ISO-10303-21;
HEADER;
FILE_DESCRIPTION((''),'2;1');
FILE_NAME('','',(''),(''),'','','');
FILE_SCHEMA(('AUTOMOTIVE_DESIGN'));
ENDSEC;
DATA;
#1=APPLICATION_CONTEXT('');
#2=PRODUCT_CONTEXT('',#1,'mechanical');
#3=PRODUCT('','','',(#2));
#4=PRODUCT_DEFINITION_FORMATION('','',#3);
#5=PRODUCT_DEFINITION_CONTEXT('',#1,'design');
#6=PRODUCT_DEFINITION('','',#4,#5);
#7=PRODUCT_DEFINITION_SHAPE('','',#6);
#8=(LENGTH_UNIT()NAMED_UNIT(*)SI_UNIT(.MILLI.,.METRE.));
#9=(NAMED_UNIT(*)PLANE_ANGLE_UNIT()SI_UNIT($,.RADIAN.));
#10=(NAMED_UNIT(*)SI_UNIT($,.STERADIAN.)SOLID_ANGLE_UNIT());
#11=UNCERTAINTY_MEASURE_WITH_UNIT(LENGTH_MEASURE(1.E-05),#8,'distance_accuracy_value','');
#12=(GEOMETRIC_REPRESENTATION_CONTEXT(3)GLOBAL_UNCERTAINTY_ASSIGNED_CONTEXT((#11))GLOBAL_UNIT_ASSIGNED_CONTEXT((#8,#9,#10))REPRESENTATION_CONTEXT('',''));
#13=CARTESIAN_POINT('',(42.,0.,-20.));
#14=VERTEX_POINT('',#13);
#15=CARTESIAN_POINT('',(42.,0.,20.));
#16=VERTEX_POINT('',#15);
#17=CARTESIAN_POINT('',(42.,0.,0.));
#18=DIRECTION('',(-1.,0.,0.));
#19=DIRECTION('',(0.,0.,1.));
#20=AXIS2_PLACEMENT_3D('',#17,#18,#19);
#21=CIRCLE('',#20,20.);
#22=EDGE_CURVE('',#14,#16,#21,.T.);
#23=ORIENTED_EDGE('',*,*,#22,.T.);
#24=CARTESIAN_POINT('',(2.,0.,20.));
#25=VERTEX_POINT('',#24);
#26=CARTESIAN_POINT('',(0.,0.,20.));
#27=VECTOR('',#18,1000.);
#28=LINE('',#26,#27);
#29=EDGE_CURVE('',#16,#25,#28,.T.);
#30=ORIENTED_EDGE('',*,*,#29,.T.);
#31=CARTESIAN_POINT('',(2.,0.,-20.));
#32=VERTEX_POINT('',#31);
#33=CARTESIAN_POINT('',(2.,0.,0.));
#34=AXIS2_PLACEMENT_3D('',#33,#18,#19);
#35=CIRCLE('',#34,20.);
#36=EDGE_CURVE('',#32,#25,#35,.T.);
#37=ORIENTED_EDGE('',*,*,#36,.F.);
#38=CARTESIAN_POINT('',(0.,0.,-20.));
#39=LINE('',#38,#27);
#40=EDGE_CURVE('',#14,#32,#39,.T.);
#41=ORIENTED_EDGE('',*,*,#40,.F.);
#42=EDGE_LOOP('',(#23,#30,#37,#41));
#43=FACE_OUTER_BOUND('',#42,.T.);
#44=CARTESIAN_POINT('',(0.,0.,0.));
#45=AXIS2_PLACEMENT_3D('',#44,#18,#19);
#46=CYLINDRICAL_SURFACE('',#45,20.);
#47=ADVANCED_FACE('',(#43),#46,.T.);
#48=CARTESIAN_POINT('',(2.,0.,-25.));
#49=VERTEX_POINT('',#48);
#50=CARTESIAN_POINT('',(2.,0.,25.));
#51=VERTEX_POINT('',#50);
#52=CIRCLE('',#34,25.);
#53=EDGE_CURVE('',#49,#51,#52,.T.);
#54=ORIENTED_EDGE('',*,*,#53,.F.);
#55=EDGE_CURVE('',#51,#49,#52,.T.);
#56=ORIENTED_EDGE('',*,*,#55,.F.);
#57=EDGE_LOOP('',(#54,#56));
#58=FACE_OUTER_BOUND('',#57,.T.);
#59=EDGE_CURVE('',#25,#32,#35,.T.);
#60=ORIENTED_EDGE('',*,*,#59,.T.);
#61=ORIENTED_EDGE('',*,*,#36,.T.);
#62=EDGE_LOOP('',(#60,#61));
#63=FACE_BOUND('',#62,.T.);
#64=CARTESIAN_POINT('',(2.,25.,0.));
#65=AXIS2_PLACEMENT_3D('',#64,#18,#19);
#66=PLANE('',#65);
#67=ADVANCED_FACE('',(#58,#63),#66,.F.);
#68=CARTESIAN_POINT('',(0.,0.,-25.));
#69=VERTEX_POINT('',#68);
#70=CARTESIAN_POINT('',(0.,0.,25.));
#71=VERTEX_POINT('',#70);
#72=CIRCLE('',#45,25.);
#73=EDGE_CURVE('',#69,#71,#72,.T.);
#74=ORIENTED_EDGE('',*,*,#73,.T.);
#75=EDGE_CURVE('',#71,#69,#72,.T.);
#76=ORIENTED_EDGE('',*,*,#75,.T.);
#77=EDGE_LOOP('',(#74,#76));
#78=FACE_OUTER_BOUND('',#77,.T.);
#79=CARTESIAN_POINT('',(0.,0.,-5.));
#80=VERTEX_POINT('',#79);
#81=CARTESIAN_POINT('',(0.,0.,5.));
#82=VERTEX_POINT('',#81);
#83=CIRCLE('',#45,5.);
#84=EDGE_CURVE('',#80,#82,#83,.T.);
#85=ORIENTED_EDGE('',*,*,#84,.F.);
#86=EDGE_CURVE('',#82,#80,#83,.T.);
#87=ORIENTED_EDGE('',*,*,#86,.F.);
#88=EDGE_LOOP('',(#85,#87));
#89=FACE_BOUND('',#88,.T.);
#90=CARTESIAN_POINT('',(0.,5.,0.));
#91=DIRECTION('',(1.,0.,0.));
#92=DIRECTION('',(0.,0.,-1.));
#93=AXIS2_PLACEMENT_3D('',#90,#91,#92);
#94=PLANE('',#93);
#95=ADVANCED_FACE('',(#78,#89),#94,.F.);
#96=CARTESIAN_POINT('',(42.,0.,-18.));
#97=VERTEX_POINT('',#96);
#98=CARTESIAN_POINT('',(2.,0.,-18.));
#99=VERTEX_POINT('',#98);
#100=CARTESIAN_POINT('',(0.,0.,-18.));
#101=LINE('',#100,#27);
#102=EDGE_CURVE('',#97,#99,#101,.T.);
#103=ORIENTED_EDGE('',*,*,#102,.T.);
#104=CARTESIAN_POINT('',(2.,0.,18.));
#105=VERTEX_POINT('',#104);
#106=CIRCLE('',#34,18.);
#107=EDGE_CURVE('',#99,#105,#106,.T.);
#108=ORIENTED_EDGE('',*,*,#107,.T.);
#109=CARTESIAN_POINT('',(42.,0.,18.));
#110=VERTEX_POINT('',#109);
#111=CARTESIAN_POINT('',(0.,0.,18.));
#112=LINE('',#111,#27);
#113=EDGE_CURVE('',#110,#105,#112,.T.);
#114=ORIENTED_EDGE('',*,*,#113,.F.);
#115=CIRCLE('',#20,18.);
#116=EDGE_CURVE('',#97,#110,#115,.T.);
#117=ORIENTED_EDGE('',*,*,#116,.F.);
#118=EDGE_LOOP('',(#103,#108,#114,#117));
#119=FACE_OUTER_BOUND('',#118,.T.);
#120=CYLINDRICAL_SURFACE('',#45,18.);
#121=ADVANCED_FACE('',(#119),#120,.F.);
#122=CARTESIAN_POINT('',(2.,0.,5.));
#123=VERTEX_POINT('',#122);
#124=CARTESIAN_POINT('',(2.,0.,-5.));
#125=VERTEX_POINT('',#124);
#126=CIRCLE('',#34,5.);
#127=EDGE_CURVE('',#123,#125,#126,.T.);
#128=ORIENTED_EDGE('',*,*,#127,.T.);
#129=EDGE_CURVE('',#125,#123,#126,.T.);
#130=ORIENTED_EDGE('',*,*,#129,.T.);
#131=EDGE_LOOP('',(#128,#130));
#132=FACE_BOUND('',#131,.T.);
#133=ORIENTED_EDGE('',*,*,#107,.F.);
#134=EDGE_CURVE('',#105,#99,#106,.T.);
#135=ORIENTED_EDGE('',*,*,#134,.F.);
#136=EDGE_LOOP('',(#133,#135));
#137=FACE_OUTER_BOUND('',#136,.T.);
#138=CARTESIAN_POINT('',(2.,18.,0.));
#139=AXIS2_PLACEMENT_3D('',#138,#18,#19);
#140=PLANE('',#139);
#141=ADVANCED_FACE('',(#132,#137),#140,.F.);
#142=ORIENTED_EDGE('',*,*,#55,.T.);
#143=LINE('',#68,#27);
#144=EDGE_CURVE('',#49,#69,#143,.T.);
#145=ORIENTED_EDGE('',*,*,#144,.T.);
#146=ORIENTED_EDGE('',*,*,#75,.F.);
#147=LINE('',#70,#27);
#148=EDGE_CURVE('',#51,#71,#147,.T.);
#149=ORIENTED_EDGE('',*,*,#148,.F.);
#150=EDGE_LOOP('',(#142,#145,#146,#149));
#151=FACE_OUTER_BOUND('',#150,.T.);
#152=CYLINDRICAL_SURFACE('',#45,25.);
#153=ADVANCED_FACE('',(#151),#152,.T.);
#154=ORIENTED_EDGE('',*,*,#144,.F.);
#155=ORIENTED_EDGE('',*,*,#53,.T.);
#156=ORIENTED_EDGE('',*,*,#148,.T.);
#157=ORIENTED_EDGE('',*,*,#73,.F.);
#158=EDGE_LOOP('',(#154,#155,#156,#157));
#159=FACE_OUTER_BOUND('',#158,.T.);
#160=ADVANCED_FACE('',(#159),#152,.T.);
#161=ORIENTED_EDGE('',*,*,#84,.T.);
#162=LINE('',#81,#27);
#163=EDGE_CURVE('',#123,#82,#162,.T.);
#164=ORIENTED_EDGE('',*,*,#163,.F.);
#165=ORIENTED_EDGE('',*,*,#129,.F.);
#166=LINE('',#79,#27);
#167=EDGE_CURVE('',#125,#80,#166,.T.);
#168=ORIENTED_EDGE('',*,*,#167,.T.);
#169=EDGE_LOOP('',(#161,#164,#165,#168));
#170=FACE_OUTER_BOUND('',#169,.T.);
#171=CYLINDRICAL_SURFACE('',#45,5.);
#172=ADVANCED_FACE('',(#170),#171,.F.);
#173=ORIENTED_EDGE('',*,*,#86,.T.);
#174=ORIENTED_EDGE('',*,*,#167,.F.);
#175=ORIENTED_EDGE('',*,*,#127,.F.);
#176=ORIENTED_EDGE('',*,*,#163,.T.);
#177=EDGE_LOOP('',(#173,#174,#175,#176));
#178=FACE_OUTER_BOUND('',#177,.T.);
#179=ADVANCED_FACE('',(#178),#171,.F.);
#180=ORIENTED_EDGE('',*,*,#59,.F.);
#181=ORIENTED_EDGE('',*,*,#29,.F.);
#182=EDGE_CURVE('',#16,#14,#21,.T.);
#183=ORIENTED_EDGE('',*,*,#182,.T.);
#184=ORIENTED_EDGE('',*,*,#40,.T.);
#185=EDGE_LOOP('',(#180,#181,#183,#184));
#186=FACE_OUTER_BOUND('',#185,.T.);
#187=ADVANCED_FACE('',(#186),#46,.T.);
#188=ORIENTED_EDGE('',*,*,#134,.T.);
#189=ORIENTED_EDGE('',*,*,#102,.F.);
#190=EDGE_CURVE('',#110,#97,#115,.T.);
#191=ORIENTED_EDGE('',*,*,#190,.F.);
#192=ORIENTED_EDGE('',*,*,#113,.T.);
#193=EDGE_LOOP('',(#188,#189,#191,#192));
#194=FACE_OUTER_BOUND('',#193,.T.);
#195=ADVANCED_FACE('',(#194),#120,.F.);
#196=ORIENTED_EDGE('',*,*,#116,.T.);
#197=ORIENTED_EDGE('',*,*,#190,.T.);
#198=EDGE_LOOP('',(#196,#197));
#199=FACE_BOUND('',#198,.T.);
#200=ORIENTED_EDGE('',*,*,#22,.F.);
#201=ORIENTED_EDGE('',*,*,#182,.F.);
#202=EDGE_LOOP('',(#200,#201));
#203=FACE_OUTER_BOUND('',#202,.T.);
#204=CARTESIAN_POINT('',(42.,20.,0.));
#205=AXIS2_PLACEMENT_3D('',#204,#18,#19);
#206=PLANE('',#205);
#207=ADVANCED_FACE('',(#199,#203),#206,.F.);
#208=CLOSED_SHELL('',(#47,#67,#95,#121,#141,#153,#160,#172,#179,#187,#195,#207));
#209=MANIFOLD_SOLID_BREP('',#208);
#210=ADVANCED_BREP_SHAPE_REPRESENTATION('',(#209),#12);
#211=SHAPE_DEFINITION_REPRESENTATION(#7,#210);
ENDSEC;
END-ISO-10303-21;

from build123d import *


with BuildPart() as part:
    # 草图1 → 旋转1 (revolve)
    with BuildSketch(Plane.XY, mode=Mode.PRIVATE) as revolve_1_sk:
        Polygon((0, 25), (2, 25), (2, 20), (42, 20), (42, 18), (2, 18), (2, 5), (0, 5), align=None)
    revolve(revolve_1_sk.sketch.rotate(Axis((0, 0, 0), (1, 0, 0)), 90), axis=Axis((0, 0, 0), (1, 0, 0)))


solid = part.part
